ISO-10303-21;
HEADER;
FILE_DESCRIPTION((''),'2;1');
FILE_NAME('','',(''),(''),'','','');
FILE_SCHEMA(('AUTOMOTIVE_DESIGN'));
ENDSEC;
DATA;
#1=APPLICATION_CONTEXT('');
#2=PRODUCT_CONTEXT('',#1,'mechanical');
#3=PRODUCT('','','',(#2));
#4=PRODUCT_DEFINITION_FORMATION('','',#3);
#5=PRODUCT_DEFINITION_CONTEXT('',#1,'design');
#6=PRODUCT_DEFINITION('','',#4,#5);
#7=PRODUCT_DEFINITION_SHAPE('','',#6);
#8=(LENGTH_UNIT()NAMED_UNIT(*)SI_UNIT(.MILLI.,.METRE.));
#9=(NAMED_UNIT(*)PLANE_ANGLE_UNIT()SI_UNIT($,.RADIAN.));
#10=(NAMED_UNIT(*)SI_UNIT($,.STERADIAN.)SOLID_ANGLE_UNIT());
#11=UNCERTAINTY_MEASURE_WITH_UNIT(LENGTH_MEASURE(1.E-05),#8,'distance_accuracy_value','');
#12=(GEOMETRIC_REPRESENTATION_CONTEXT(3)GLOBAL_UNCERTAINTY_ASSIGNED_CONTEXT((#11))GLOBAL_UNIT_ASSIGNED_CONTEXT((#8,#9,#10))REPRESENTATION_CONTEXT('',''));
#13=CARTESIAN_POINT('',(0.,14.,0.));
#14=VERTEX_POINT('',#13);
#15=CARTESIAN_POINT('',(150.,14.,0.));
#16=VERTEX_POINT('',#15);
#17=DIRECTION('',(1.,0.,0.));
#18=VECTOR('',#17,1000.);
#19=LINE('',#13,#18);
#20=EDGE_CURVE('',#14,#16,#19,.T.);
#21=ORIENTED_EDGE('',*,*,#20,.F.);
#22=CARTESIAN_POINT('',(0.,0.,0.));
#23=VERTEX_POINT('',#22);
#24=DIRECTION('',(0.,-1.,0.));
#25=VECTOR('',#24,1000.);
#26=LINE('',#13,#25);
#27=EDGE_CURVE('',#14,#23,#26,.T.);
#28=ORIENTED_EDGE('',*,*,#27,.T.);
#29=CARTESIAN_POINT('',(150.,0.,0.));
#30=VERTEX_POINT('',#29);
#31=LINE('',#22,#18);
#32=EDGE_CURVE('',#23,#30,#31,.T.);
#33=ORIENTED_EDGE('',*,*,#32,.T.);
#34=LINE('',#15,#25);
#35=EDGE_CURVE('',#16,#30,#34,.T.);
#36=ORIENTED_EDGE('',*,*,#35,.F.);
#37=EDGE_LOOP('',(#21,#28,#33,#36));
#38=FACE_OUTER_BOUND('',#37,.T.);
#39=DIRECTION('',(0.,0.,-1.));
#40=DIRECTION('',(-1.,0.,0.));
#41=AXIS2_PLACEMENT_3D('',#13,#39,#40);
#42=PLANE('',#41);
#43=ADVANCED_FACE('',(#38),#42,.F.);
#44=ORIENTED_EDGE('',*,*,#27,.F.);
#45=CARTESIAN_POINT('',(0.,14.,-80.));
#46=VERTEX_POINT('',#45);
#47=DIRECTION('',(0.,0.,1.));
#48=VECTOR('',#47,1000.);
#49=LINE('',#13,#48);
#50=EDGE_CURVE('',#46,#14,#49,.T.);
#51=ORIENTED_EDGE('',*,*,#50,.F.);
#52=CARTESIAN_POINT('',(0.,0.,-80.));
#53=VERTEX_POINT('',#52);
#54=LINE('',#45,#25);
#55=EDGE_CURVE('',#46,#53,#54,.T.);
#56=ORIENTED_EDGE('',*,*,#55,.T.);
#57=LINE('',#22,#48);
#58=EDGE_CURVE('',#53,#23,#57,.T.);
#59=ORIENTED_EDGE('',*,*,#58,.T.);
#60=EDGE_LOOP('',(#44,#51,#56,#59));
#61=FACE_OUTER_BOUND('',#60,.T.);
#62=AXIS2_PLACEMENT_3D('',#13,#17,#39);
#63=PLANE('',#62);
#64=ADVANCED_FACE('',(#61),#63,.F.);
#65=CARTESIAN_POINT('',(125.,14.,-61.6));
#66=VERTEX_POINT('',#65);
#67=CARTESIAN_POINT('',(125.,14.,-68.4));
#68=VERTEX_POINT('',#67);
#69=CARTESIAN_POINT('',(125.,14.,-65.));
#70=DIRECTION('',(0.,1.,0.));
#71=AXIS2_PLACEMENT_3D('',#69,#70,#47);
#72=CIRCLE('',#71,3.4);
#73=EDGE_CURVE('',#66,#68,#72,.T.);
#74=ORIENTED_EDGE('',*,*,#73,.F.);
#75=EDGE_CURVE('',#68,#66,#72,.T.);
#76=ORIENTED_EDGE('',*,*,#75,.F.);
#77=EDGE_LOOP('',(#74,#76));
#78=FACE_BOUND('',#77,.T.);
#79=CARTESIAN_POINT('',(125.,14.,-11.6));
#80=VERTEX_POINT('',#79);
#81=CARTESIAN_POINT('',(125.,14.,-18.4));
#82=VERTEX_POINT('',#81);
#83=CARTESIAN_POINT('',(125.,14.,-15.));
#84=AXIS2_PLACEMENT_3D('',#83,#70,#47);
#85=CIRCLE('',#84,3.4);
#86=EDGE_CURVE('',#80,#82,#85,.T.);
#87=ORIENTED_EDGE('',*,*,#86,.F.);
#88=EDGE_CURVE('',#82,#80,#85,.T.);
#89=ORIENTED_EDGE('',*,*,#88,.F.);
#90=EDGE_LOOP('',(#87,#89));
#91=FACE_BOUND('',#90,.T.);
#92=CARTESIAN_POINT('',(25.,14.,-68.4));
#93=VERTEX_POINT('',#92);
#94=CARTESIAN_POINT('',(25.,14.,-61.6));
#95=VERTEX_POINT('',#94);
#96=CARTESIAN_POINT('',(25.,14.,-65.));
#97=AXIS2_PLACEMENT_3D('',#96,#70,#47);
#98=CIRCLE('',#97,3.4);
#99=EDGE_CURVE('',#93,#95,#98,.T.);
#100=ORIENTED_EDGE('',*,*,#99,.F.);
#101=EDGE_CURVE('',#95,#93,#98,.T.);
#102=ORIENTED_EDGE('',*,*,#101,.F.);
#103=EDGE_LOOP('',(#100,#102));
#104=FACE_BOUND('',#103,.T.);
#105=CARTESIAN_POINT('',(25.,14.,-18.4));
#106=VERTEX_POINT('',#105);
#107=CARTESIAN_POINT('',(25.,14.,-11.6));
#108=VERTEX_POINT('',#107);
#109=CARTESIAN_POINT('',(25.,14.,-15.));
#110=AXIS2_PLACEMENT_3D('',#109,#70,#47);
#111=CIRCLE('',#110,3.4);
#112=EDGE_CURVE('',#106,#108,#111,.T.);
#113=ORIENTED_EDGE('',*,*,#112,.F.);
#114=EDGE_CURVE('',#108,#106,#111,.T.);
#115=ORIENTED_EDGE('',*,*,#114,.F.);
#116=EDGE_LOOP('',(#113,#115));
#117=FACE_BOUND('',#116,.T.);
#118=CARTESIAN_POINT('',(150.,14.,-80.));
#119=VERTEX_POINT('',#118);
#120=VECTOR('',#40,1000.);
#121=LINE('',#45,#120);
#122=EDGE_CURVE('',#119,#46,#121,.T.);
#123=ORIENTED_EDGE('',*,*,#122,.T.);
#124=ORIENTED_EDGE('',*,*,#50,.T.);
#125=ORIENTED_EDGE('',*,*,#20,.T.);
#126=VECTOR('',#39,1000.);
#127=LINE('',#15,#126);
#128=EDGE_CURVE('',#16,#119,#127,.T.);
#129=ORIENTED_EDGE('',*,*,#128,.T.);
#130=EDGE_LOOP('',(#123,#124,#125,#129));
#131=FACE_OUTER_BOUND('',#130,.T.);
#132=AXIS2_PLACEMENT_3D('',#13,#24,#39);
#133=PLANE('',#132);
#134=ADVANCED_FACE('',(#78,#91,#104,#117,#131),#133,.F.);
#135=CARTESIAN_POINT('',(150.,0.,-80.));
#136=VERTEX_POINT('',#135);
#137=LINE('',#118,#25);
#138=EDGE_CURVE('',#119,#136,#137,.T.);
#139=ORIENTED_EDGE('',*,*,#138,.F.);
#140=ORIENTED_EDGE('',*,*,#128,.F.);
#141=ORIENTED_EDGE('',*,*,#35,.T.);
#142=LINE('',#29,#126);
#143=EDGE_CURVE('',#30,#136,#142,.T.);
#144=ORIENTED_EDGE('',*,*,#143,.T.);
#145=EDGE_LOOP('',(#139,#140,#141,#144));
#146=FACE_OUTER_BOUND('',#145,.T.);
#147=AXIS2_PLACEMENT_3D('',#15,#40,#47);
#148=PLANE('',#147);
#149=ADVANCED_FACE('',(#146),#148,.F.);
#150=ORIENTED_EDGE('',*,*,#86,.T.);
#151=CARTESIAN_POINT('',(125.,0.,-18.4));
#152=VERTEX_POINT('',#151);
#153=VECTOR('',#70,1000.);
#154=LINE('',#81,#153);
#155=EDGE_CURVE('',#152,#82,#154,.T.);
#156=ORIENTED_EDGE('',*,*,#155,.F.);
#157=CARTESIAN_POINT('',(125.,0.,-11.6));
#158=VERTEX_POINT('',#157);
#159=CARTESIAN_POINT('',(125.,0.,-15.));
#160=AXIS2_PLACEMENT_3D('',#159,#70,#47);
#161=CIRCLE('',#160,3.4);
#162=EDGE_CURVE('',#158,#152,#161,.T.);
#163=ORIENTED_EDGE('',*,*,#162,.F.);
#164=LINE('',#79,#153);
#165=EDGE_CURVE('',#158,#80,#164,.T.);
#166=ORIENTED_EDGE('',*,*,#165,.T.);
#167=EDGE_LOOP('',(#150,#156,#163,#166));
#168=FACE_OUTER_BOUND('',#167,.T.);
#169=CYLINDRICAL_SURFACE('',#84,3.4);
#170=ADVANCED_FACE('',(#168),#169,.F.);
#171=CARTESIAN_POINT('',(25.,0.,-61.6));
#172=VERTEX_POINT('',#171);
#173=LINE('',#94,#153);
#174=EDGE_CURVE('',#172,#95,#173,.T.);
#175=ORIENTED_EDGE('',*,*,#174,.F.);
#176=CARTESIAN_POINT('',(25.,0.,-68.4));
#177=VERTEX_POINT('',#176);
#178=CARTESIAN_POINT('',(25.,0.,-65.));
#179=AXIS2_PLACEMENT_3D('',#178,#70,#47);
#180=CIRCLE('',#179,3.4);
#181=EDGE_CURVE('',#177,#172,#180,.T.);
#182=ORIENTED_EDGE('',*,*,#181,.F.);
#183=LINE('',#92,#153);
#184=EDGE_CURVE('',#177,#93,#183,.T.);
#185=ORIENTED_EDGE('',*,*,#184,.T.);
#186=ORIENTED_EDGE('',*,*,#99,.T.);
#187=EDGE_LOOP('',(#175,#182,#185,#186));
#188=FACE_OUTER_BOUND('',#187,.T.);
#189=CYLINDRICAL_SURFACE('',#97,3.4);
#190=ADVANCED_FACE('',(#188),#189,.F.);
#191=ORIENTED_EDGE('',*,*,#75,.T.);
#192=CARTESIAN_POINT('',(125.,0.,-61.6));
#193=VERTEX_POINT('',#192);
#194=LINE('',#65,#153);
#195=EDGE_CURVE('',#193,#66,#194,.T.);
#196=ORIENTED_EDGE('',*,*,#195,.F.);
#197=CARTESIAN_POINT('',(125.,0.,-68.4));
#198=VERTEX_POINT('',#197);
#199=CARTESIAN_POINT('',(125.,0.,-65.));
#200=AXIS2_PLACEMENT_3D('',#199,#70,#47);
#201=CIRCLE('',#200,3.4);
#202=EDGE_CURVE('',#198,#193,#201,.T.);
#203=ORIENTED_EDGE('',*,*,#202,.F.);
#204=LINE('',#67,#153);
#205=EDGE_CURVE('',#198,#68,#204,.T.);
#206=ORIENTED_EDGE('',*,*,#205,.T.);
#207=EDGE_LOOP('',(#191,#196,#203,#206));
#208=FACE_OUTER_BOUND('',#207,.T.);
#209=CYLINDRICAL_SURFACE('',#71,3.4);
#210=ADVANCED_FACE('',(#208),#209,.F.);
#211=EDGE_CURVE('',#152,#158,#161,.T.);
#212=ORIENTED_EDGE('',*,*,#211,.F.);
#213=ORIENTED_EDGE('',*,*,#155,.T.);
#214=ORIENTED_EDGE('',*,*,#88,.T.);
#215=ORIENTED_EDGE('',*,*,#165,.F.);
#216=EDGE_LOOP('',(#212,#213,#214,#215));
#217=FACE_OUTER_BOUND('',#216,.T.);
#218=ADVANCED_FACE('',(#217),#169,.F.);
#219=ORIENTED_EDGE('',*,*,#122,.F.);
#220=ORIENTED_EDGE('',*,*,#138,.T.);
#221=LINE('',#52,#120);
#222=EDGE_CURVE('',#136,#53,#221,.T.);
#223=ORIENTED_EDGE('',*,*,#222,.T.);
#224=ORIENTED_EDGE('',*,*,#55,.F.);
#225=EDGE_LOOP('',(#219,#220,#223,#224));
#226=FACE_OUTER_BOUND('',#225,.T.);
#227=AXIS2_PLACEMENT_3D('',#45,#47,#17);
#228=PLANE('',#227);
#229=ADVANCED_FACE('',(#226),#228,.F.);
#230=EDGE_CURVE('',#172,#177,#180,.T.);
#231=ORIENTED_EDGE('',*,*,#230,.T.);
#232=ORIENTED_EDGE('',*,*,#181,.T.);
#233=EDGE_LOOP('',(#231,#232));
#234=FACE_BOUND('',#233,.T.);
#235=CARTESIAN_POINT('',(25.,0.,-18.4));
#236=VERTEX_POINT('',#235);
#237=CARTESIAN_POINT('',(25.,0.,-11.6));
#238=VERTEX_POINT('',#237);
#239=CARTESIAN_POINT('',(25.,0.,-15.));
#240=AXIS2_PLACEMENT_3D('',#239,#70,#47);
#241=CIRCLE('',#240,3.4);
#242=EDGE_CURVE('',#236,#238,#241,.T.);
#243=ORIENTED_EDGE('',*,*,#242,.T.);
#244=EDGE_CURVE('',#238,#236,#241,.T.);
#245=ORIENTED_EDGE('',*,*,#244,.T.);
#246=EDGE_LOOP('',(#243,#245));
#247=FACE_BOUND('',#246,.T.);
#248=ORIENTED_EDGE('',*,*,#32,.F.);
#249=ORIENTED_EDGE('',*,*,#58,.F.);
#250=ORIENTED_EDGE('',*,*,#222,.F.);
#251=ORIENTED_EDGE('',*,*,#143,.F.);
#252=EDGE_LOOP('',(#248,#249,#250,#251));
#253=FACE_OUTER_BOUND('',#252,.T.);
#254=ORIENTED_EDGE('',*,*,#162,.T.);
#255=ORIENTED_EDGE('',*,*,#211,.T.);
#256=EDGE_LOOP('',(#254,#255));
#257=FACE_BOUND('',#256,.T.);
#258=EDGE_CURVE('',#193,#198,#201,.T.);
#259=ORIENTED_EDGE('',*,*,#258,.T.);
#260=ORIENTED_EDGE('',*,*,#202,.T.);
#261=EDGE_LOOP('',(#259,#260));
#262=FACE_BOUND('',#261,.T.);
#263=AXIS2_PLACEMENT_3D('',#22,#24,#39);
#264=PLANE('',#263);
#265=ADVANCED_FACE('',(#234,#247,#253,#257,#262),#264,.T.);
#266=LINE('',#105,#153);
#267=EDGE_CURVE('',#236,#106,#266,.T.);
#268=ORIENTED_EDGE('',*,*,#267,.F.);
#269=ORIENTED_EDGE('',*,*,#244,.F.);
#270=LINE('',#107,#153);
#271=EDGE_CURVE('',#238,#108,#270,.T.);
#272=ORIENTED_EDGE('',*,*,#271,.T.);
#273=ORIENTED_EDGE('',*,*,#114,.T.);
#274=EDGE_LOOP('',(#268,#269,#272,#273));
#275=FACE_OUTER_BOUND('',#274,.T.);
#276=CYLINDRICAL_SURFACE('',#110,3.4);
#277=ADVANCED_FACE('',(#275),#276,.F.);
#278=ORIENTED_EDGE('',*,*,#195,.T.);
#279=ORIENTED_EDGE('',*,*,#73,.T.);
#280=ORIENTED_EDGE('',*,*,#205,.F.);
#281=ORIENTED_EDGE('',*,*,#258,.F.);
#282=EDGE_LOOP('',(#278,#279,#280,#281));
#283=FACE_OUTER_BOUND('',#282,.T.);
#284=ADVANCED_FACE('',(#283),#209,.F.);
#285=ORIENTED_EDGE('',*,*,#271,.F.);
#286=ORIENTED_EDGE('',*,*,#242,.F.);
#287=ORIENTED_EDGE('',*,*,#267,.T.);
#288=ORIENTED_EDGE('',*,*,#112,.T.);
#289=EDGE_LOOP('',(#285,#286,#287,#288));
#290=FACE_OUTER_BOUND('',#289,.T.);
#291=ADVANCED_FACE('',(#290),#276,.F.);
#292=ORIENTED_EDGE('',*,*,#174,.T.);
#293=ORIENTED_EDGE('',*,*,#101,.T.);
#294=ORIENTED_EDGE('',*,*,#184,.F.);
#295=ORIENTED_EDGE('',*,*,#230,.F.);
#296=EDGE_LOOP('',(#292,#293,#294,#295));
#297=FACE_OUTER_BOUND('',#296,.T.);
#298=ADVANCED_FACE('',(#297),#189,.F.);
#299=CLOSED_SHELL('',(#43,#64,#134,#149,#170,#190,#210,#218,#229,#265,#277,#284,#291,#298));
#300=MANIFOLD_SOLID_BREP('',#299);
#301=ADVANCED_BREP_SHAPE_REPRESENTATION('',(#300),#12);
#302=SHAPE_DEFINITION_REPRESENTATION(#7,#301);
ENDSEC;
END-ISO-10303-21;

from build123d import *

# Parameters (mm, degrees)
SKETCH1_W           = 150
SKETCH1_H           = 80
BOSS_EXTRUDE1_DEPTH = 14
M8_TAPPED_HOLE1_D   = 6.8


with BuildPart() as part:
    # Sketch1 → Boss-Extrude1 (new body)
    with BuildSketch(Plane(origin=(0, 0, 0), x_dir=(1, 0, 0), z_dir=(0, 1, 0))):
        with Locations((75, 40)):
            Rectangle(SKETCH1_W, SKETCH1_H)
    extrude(amount=BOSS_EXTRUDE1_DEPTH)

    # M8 Tapped Hole1 (through all)
    with Locations(Plane(origin=(0, 14, 0), x_dir=(-1, 0, 0), z_dir=(0, 1, 0))):
        with Locations((-25, -65), (-25, -15), (-125, -15), (-125, -65)):
            Hole(M8_TAPPED_HOLE1_D / 2)


solid = part.part
